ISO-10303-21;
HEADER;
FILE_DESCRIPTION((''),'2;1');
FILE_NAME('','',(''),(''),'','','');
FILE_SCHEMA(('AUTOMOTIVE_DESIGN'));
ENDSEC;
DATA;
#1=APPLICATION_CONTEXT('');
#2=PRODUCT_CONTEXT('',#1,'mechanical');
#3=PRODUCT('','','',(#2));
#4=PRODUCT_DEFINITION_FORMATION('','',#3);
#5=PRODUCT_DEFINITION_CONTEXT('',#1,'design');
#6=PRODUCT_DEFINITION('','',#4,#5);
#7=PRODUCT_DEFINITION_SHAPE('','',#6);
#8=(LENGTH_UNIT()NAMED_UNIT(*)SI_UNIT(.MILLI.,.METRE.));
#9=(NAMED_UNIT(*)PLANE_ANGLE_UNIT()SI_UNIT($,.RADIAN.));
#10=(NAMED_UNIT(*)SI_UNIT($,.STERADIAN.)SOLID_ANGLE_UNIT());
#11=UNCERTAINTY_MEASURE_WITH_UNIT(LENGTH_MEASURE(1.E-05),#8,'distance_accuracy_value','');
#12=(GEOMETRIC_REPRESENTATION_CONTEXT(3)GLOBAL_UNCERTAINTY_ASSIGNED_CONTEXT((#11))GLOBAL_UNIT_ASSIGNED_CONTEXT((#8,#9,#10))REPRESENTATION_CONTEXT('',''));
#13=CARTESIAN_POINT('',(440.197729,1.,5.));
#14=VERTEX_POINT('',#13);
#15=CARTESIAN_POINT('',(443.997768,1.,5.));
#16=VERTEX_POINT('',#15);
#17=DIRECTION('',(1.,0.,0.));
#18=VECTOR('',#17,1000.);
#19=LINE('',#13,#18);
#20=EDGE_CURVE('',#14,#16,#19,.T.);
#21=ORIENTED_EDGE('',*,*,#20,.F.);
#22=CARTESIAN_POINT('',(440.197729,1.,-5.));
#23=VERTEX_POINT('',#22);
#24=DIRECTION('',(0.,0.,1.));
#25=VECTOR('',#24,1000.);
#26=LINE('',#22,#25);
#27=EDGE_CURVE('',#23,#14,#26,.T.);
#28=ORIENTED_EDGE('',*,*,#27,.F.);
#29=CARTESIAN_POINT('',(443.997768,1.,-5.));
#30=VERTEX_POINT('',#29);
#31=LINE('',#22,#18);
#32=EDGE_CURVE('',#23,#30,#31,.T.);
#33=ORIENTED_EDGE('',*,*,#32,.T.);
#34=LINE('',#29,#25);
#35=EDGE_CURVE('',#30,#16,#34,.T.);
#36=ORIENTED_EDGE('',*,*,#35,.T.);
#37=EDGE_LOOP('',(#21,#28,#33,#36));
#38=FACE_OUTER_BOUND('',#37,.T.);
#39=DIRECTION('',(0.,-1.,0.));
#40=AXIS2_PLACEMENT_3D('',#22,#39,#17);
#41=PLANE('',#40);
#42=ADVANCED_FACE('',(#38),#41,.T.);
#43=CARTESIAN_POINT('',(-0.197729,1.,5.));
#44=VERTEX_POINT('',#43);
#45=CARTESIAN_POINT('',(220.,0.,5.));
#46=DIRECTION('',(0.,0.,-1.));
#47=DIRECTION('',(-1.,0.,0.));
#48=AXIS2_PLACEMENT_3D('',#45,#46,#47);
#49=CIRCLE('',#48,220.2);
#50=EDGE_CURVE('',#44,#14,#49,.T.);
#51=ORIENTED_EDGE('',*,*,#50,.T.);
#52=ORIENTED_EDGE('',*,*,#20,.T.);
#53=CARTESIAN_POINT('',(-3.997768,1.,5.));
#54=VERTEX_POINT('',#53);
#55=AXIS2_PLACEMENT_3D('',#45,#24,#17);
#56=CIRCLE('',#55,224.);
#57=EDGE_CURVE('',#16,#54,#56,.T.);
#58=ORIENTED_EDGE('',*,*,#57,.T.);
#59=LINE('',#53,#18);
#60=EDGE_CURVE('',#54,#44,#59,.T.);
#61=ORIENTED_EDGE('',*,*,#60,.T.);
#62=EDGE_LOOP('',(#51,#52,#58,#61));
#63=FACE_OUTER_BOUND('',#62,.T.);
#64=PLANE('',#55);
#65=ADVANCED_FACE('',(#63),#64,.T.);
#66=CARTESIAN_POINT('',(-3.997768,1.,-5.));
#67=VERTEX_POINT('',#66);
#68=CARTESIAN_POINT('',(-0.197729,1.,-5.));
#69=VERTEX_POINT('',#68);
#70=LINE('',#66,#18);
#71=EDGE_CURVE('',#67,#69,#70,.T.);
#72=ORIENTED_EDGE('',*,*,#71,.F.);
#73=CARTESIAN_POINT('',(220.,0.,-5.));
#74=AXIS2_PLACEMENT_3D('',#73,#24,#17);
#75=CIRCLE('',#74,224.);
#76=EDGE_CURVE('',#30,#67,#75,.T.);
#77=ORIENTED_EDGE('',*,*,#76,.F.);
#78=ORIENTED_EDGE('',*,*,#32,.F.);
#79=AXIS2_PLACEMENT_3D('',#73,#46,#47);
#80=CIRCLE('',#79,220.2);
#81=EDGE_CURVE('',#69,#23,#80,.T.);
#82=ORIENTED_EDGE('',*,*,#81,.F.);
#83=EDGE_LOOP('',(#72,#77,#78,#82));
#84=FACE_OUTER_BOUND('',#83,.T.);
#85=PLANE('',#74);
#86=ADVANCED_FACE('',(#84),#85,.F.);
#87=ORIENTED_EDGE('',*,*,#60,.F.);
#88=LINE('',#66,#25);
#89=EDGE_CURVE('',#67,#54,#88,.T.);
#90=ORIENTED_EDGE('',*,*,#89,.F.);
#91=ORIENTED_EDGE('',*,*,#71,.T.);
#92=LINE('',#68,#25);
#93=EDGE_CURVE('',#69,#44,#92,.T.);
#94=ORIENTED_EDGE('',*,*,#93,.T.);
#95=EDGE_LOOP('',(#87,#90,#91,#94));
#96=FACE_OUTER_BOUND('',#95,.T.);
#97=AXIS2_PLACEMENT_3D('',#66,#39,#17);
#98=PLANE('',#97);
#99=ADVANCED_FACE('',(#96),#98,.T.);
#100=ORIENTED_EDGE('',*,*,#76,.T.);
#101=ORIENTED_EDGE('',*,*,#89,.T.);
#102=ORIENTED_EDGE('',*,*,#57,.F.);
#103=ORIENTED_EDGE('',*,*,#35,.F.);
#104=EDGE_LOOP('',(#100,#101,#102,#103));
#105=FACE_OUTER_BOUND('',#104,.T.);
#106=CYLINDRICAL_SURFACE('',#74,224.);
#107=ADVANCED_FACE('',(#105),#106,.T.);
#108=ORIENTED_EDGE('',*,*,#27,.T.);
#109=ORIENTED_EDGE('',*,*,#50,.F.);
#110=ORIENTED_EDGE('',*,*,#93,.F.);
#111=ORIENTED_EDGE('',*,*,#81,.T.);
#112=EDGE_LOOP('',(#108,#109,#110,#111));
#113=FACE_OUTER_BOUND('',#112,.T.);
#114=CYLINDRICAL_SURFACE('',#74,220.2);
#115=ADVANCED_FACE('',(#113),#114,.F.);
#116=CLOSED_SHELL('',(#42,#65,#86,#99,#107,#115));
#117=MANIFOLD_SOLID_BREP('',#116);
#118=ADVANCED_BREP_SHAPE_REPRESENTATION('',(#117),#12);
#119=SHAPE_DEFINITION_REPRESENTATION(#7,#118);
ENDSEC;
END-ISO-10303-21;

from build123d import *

# Parameters (mm, degrees)
EXTRUDE_1_DEPTH = 5


with BuildPart() as part:
    # 草图1 → 凸台-拉伸1 (new, symmetric)
    with BuildSketch(Plane.XY):
        with BuildLine():
            Line((-3.997767846, 1), (-0.197729325, 1))
            ThreePointArc((-0.197729325, 1), (220, 220.2), (440.197729325, 1))
            Line((440.197729325, 1), (443.997767846, 1))
            ThreePointArc((443.997767846, 1), (220, 224), (-3.997767846, 1))
        make_face()
    extrude(amount=EXTRUDE_1_DEPTH, both=True)


solid = part.part
